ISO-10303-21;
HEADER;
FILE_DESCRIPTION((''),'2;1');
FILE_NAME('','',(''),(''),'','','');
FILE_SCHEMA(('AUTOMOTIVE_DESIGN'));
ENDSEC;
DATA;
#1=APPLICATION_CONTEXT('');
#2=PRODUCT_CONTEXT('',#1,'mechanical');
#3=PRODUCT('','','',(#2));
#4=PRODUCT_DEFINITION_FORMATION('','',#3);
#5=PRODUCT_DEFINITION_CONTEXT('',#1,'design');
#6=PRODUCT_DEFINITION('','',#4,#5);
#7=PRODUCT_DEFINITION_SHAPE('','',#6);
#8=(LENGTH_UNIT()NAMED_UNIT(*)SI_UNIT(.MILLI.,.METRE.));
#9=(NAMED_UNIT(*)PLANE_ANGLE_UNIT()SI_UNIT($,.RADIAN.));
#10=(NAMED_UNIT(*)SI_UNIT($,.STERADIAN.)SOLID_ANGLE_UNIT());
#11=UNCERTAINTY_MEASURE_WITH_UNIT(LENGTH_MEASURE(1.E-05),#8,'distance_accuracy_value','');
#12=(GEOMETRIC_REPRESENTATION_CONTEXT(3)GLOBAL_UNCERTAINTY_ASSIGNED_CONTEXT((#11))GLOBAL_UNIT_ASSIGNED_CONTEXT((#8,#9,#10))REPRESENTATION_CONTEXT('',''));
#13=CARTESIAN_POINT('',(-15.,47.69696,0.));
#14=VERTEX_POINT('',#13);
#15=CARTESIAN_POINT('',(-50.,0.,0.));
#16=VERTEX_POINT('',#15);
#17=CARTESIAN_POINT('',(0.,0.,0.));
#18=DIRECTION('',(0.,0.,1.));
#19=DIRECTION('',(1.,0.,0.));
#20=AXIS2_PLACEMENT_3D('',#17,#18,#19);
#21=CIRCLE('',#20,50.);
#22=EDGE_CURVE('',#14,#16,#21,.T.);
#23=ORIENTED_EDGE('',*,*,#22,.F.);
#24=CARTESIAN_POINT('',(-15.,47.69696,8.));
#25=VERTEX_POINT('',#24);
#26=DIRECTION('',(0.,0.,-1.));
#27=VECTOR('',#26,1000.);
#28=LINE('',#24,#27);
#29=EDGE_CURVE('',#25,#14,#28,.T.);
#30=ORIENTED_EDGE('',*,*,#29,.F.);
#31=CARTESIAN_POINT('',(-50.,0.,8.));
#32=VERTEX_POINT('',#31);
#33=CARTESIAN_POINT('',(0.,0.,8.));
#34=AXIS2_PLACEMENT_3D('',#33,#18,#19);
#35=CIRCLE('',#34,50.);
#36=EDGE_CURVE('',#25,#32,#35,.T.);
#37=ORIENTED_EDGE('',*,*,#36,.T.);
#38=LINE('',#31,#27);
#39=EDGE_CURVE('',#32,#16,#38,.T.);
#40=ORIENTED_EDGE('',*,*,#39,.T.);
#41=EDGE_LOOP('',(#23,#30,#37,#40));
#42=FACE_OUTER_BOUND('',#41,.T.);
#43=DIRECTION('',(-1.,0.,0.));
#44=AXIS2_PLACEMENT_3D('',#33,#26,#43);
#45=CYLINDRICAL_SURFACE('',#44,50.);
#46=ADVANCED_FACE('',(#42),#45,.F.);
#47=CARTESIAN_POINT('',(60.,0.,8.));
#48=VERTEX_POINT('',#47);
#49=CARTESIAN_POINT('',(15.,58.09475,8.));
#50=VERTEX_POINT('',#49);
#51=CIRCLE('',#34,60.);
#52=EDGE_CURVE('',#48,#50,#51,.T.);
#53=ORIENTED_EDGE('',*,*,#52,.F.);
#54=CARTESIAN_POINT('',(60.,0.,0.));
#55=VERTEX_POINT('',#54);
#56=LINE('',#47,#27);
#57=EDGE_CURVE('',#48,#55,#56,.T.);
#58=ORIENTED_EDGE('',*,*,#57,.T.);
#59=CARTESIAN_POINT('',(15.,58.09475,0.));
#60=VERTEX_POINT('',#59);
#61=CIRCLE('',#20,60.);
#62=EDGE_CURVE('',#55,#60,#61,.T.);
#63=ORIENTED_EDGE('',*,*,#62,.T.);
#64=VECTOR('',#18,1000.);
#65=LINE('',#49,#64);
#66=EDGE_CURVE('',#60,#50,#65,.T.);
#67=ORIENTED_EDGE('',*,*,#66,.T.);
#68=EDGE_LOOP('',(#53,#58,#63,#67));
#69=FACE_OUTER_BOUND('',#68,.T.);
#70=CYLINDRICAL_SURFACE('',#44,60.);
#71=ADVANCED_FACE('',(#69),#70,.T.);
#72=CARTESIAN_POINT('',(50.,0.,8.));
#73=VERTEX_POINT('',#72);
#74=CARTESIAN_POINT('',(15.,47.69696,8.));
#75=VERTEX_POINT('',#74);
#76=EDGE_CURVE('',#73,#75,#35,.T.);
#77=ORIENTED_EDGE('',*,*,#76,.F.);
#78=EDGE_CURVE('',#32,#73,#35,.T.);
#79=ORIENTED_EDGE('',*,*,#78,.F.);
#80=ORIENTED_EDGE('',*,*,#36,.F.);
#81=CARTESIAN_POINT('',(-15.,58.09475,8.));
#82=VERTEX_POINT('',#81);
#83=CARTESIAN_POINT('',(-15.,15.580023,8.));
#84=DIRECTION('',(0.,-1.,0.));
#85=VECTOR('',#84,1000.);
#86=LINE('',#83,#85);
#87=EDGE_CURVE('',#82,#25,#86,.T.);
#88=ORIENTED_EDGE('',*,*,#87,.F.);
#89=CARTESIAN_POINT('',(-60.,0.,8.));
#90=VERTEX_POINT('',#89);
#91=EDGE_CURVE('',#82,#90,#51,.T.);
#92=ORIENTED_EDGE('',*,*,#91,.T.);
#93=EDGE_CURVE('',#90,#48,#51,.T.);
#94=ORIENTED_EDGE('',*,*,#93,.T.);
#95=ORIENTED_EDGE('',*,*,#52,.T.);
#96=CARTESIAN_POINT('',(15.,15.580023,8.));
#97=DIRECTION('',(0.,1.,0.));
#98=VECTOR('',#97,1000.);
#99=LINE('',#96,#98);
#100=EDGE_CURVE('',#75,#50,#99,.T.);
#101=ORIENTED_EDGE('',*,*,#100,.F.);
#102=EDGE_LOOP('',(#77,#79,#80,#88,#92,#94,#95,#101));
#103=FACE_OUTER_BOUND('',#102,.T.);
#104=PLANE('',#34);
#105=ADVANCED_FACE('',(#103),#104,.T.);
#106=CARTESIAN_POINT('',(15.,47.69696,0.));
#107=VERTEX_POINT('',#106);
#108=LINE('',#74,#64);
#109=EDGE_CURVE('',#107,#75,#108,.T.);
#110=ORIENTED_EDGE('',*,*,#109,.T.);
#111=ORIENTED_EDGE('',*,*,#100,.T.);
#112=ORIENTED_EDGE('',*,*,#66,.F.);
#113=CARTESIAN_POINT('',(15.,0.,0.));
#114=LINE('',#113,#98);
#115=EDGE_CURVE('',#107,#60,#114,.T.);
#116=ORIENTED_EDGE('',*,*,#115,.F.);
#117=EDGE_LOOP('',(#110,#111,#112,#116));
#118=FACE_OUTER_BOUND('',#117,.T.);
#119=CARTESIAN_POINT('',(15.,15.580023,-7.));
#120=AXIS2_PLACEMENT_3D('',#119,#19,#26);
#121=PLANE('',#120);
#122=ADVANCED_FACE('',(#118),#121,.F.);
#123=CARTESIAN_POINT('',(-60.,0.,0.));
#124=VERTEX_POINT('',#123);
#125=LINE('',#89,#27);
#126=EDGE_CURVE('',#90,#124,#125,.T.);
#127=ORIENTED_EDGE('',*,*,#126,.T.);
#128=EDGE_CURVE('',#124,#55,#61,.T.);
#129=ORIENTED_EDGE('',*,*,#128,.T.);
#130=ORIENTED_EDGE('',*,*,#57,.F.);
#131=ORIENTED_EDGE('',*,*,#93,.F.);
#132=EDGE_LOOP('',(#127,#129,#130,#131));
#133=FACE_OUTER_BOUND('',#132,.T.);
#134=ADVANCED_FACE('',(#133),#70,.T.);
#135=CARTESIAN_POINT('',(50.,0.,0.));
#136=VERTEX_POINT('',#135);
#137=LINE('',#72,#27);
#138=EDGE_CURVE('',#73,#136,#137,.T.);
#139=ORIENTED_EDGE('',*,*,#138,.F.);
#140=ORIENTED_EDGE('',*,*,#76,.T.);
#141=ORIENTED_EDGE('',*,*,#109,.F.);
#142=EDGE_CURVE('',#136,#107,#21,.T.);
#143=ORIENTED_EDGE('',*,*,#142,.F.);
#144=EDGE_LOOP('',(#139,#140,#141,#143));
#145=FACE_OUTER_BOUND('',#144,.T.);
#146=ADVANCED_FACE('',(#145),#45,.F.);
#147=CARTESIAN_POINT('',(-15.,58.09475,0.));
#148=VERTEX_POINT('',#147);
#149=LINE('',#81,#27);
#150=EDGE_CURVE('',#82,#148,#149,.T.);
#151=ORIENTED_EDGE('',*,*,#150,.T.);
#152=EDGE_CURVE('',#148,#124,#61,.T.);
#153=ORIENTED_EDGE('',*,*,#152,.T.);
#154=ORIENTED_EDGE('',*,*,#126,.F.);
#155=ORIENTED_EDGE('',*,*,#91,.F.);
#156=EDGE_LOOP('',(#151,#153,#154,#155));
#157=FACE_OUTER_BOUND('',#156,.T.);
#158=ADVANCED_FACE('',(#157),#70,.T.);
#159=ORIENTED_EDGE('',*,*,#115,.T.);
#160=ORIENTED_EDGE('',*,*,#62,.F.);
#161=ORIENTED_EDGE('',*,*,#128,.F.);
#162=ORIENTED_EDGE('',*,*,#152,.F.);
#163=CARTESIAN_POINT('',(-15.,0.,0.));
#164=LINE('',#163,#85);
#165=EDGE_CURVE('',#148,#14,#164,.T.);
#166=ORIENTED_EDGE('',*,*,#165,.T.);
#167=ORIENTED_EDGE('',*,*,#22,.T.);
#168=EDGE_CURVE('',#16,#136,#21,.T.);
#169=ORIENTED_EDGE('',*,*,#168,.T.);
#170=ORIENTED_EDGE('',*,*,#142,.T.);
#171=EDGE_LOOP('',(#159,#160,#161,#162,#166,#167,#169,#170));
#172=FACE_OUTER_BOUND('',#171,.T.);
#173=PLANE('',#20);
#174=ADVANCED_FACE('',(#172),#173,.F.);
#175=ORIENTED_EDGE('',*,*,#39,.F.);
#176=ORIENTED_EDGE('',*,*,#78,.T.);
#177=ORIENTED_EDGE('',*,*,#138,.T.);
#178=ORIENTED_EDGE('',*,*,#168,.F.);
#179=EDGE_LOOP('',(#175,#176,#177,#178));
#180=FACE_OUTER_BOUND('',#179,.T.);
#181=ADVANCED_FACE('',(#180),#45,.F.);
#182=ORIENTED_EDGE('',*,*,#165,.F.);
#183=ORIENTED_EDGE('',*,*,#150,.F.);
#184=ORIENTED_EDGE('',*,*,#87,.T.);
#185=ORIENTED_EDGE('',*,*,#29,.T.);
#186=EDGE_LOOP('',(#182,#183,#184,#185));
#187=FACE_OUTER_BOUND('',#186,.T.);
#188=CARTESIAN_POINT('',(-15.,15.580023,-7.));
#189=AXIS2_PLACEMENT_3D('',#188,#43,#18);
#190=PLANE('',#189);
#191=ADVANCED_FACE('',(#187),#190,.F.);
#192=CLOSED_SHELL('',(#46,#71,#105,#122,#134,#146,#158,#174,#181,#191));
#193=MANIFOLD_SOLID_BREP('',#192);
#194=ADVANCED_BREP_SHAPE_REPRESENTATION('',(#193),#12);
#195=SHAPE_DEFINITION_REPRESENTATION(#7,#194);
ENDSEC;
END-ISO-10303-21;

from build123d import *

# Parameters (mm, degrees)
SKETCH1_R           = 60
SKETCH1_R_2         = 50
BOSS_EXTRUDE1_DEPTH = 8
SKETCH2_W           = 30
SKETCH2_H           = 71.834610917
CUT_EXTRUDE1_DEPTH  = 15


with BuildPart() as part:
    # Sketch1 → Boss-Extrude1 (new body)
    with BuildSketch(Plane.XY):
        Circle(SKETCH1_R)
        Circle(SKETCH1_R_2, mode=Mode.SUBTRACT)
    extrude(amount=BOSS_EXTRUDE1_DEPTH)

    # Sketch2 → Cut-Extrude1 (cut)
    with BuildSketch(Plane.XY.offset(8)):
        with Locations((0, 51.497328688)):
            Rectangle(SKETCH2_W, SKETCH2_H)
    extrude(amount=-CUT_EXTRUDE1_DEPTH, mode=Mode.SUBTRACT)


solid = part.part
